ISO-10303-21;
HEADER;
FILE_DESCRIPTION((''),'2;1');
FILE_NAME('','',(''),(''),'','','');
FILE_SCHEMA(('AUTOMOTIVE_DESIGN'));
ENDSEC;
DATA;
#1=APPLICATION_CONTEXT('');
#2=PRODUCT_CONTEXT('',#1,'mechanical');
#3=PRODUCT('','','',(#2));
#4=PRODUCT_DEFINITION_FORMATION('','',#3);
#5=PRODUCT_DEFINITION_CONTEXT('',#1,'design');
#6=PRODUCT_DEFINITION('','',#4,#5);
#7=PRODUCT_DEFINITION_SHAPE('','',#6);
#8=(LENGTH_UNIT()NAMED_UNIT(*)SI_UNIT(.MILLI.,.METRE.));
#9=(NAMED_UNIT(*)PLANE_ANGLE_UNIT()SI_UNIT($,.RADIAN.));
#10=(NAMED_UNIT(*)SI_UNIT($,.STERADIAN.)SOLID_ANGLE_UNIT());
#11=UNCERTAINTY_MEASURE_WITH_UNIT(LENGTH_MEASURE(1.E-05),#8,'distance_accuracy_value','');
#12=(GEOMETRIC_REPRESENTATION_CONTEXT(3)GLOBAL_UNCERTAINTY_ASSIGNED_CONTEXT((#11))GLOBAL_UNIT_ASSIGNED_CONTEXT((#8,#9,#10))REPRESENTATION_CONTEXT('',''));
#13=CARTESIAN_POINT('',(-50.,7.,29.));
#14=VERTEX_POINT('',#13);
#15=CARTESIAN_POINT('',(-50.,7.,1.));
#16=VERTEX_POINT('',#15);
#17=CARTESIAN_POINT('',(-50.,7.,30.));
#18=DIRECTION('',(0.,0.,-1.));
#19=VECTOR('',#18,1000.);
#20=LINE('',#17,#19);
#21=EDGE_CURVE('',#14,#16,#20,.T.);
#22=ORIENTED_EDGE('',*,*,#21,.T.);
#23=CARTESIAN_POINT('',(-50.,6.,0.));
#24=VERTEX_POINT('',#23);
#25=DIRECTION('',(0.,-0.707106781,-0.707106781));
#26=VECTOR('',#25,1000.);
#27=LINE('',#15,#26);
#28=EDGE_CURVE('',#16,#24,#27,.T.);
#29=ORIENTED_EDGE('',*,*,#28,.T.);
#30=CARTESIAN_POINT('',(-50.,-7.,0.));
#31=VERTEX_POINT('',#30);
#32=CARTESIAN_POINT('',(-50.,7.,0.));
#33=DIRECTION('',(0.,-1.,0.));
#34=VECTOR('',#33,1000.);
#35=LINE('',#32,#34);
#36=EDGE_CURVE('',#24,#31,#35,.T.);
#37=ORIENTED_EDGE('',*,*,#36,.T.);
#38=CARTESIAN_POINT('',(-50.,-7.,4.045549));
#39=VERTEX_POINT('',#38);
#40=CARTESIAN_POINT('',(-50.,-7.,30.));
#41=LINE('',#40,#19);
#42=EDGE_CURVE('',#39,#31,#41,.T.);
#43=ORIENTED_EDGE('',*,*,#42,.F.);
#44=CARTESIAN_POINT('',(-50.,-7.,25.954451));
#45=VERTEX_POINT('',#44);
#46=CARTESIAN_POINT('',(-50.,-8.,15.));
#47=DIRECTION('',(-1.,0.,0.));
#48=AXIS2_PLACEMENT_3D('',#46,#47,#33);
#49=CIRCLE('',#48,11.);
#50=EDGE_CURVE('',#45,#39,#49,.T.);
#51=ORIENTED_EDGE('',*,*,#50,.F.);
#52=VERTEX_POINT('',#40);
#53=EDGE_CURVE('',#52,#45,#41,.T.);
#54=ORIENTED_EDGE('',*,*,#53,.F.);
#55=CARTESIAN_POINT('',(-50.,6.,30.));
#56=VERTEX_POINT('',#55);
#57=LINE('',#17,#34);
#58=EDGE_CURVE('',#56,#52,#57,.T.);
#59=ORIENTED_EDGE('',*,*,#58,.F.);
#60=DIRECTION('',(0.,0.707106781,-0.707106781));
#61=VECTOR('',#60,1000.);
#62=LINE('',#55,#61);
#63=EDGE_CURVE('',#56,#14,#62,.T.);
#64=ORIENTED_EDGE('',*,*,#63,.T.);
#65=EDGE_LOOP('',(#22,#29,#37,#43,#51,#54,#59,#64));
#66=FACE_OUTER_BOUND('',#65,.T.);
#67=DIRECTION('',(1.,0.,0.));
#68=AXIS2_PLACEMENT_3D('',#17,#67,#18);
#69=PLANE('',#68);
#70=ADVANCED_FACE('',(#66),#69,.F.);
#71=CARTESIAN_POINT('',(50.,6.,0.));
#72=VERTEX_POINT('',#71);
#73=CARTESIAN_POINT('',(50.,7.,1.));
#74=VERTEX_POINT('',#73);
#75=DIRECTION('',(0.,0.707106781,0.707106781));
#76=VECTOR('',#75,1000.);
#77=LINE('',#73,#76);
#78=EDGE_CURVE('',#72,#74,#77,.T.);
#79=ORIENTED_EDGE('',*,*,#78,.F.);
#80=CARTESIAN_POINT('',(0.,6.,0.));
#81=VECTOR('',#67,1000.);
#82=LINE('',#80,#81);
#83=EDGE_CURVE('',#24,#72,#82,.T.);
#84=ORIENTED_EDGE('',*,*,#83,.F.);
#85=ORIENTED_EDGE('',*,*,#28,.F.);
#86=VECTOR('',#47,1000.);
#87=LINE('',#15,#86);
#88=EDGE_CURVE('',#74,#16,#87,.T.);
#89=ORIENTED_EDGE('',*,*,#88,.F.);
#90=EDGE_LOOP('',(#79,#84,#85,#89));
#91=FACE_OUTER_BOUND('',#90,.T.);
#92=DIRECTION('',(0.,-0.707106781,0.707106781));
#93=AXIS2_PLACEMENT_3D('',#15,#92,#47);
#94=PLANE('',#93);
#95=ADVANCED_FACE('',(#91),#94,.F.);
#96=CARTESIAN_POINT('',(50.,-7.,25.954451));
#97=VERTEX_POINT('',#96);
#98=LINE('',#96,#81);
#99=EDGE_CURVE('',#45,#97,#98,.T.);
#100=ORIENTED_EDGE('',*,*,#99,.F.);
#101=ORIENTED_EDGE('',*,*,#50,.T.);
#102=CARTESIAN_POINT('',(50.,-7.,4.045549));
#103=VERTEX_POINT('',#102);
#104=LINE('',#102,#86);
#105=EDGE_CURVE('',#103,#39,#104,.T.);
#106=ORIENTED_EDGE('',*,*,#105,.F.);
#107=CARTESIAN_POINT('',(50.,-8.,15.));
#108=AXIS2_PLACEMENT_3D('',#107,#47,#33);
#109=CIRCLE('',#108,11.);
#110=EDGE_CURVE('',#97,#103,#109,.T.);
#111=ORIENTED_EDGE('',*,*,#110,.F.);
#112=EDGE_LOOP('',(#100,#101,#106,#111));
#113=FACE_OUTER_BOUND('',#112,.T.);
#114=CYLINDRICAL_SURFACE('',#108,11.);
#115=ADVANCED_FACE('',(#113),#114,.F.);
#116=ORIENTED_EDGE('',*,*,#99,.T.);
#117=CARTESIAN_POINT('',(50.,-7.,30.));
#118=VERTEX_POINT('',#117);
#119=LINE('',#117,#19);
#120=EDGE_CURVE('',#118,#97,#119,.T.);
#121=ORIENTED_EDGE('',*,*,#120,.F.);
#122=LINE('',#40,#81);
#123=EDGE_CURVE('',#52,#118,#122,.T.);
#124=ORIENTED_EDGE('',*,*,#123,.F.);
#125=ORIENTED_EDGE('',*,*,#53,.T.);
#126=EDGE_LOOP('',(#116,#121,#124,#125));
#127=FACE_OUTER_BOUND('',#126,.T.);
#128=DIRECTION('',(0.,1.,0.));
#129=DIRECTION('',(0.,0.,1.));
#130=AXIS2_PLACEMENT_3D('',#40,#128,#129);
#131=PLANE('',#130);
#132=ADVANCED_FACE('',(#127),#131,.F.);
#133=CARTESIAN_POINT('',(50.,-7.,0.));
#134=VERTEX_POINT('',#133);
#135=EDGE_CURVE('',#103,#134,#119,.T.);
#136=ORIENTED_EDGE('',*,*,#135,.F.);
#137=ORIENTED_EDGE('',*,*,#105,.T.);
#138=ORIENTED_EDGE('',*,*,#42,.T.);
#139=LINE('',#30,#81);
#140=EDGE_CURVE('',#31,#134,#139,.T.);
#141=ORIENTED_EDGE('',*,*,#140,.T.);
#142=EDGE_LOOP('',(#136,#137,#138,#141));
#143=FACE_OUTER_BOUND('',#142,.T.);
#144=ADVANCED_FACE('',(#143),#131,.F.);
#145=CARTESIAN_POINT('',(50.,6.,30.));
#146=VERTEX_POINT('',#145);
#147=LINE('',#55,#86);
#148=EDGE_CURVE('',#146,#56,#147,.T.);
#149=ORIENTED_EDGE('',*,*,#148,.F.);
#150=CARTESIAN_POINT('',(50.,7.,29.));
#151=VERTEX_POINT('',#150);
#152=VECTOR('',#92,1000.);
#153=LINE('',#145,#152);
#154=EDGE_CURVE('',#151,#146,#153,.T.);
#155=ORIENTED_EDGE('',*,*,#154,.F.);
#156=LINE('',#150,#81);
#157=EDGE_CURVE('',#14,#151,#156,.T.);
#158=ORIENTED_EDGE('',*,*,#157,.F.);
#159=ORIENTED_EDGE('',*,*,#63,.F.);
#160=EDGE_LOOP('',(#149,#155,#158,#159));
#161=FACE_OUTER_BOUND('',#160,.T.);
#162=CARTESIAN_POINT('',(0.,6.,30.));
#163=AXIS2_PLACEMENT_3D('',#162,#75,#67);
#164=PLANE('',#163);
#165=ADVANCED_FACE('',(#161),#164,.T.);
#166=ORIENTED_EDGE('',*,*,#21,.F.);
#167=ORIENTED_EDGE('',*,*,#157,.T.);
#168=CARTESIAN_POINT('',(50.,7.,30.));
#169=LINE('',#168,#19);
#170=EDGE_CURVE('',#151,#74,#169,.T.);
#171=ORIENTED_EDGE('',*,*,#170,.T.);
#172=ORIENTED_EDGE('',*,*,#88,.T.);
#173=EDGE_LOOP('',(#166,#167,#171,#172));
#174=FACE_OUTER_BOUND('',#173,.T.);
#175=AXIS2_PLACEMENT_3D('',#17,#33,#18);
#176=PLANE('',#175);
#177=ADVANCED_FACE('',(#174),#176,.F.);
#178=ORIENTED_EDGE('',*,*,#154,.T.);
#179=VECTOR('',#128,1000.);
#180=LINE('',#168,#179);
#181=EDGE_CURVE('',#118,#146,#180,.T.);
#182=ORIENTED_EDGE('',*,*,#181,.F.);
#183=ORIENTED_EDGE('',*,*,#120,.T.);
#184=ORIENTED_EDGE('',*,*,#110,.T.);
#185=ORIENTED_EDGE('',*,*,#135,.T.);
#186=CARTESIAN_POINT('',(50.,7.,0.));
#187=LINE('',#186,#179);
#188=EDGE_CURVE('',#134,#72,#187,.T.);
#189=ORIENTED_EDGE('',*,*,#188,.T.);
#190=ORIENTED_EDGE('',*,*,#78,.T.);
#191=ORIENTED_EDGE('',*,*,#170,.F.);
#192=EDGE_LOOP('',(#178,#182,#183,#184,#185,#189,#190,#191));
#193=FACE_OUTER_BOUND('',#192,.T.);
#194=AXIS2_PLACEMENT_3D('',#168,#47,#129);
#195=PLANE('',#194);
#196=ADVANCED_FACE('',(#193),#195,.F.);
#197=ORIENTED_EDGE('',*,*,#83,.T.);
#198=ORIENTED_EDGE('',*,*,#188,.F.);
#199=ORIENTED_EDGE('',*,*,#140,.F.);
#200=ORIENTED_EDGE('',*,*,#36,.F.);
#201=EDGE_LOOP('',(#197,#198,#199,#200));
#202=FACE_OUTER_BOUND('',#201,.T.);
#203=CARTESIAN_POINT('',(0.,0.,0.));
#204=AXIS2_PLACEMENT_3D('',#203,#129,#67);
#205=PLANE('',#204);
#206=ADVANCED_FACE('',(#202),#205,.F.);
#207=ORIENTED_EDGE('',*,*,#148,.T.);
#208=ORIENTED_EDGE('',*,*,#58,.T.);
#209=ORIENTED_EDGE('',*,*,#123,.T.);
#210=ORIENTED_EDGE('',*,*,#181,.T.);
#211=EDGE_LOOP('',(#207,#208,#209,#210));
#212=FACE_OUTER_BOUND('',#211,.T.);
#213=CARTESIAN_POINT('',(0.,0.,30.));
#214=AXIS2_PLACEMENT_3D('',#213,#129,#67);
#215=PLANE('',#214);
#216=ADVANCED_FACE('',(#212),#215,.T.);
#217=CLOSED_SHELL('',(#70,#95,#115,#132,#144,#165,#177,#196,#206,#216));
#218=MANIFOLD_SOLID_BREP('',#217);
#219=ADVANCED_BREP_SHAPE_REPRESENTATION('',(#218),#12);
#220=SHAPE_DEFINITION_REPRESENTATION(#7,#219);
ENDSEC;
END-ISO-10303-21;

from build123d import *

# Parameters (mm, degrees)
SKETCH1_W           = 100
SKETCH1_H           = 14
BOSS_EXTRUDE1_DEPTH = 30
SKETCH2_R           = 11
CUT_EXTRUDE1_DEPTH  = 105.637469388
CHAMFER1_SIZE       = 1


with BuildPart() as part:
    # Sketch1 → Boss-Extrude1 (new body)
    with BuildSketch(Plane.XY):
        Rectangle(SKETCH1_W, SKETCH1_H)
    extrude(amount=BOSS_EXTRUDE1_DEPTH)

    # Sketch2 → Cut-Extrude1 (cut, through all)
    with BuildSketch(Plane.ZY.offset(50)):
        with Locations((15, -8)):
            Circle(SKETCH2_R)
    extrude(amount=-CUT_EXTRUDE1_DEPTH, mode=Mode.SUBTRACT)

    # Chamfer1
    chamfer1_edges = [part.edges().sort_by_distance(p)[0] for p in [
        (0, 7, 0),
        (0, 7, 30),
    ]]
    chamfer(chamfer1_edges, length=CHAMFER1_SIZE)


solid = part.part
